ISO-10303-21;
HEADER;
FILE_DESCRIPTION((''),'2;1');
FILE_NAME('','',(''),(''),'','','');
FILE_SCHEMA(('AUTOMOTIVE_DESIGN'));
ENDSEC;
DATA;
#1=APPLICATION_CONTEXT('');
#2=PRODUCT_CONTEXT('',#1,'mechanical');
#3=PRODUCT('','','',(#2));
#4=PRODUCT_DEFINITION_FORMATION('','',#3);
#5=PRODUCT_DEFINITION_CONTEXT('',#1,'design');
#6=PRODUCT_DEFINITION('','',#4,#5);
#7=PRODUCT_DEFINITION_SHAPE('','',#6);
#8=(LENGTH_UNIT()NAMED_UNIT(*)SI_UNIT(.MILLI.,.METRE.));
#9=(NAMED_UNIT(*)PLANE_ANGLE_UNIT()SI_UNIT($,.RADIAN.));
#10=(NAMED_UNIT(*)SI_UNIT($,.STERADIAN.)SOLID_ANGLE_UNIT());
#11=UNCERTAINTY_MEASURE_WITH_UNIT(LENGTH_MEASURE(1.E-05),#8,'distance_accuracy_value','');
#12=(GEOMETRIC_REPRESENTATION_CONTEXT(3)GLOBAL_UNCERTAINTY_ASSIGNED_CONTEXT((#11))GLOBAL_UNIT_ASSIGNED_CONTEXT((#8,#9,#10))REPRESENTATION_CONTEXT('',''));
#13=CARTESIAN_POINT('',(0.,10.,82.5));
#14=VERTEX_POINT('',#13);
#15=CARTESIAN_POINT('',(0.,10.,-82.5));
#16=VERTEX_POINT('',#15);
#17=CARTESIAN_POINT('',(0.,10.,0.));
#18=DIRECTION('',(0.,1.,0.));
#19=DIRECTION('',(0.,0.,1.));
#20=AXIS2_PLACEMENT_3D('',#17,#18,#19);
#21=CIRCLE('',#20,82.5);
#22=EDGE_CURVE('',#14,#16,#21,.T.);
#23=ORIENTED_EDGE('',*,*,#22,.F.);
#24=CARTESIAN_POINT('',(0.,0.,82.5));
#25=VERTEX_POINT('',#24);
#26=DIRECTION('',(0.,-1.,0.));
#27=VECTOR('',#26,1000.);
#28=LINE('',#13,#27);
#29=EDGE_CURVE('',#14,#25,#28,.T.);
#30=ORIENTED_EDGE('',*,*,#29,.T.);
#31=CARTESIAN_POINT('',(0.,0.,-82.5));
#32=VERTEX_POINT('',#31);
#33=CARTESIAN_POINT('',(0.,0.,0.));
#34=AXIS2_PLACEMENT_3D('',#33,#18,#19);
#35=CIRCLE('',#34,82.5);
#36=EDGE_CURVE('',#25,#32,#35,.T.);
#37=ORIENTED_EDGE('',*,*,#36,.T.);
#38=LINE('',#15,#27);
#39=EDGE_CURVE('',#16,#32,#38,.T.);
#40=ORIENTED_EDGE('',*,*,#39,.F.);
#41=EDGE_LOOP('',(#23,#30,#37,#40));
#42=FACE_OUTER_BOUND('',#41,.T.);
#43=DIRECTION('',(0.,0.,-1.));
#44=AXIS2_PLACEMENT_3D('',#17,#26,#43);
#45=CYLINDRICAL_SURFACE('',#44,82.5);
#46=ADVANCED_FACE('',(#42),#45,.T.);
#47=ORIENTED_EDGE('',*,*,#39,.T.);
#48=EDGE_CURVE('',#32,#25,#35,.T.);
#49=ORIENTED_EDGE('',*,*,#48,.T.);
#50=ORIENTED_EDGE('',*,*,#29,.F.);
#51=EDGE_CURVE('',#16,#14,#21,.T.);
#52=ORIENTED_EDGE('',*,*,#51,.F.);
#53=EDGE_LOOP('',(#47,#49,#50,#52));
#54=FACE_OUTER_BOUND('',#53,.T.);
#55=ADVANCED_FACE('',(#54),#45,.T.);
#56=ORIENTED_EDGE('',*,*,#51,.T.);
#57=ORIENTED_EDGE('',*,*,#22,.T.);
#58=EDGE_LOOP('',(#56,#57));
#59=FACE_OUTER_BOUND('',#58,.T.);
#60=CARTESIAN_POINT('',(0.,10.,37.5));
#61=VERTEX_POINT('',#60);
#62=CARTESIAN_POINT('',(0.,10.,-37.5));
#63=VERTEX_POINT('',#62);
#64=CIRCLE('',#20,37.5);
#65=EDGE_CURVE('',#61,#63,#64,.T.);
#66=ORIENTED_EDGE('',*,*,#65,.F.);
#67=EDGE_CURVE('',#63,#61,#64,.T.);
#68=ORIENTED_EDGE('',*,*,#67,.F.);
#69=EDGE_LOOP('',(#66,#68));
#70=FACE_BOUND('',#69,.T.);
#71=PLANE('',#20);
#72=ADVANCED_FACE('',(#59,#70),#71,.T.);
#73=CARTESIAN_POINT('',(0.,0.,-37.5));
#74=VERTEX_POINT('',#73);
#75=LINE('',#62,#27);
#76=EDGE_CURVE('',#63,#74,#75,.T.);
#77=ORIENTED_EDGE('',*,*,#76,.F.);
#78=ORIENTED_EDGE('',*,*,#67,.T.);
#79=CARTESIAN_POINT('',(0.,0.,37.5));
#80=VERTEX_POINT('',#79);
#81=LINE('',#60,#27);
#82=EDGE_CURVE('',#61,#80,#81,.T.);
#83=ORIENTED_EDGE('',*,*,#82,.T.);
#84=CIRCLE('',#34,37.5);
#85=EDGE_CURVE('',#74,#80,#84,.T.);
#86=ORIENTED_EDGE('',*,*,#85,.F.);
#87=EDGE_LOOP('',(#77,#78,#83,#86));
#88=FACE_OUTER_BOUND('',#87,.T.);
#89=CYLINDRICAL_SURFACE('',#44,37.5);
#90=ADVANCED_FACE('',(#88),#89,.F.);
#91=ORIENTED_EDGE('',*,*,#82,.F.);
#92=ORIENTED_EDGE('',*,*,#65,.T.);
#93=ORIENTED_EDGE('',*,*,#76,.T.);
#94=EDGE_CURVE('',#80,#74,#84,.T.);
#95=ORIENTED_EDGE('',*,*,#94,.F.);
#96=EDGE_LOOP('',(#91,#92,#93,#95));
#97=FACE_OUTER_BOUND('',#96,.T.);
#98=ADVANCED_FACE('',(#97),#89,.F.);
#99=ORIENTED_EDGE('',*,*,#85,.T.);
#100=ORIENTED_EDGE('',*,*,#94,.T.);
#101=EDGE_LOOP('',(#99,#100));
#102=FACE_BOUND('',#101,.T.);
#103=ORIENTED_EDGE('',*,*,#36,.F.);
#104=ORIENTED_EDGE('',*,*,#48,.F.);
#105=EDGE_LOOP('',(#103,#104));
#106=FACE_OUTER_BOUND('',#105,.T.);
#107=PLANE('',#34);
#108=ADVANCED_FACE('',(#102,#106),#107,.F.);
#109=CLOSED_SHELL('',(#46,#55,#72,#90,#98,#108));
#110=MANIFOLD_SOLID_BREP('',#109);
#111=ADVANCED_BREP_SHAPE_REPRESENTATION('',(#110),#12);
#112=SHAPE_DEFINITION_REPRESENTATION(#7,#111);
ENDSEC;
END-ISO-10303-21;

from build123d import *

# Parameters (mm, degrees)
WASHER_PROFILE_165X_75_R   = 82.5
WASHER_PROFILE_165X_75_R_2 = 37.5
WASHER_BODY_10MM_DEPTH     = 10


with BuildPart() as part:
    # Washer Profile Ø165xØ75 → Washer Body 10mm (new body)
    with BuildSketch(Plane(origin=(0, 0, 0), x_dir=(1, 0, 0), z_dir=(0, 1, 0))):
        with Locations(Location((0, 0, 0), (0, 0, 270))):
            Circle(WASHER_PROFILE_165X_75_R)
        with Locations(Location((0, 0, 0), (0, 0, 270))):
            Circle(WASHER_PROFILE_165X_75_R_2, mode=Mode.SUBTRACT)
    extrude(amount=WASHER_BODY_10MM_DEPTH)


solid = part.part
